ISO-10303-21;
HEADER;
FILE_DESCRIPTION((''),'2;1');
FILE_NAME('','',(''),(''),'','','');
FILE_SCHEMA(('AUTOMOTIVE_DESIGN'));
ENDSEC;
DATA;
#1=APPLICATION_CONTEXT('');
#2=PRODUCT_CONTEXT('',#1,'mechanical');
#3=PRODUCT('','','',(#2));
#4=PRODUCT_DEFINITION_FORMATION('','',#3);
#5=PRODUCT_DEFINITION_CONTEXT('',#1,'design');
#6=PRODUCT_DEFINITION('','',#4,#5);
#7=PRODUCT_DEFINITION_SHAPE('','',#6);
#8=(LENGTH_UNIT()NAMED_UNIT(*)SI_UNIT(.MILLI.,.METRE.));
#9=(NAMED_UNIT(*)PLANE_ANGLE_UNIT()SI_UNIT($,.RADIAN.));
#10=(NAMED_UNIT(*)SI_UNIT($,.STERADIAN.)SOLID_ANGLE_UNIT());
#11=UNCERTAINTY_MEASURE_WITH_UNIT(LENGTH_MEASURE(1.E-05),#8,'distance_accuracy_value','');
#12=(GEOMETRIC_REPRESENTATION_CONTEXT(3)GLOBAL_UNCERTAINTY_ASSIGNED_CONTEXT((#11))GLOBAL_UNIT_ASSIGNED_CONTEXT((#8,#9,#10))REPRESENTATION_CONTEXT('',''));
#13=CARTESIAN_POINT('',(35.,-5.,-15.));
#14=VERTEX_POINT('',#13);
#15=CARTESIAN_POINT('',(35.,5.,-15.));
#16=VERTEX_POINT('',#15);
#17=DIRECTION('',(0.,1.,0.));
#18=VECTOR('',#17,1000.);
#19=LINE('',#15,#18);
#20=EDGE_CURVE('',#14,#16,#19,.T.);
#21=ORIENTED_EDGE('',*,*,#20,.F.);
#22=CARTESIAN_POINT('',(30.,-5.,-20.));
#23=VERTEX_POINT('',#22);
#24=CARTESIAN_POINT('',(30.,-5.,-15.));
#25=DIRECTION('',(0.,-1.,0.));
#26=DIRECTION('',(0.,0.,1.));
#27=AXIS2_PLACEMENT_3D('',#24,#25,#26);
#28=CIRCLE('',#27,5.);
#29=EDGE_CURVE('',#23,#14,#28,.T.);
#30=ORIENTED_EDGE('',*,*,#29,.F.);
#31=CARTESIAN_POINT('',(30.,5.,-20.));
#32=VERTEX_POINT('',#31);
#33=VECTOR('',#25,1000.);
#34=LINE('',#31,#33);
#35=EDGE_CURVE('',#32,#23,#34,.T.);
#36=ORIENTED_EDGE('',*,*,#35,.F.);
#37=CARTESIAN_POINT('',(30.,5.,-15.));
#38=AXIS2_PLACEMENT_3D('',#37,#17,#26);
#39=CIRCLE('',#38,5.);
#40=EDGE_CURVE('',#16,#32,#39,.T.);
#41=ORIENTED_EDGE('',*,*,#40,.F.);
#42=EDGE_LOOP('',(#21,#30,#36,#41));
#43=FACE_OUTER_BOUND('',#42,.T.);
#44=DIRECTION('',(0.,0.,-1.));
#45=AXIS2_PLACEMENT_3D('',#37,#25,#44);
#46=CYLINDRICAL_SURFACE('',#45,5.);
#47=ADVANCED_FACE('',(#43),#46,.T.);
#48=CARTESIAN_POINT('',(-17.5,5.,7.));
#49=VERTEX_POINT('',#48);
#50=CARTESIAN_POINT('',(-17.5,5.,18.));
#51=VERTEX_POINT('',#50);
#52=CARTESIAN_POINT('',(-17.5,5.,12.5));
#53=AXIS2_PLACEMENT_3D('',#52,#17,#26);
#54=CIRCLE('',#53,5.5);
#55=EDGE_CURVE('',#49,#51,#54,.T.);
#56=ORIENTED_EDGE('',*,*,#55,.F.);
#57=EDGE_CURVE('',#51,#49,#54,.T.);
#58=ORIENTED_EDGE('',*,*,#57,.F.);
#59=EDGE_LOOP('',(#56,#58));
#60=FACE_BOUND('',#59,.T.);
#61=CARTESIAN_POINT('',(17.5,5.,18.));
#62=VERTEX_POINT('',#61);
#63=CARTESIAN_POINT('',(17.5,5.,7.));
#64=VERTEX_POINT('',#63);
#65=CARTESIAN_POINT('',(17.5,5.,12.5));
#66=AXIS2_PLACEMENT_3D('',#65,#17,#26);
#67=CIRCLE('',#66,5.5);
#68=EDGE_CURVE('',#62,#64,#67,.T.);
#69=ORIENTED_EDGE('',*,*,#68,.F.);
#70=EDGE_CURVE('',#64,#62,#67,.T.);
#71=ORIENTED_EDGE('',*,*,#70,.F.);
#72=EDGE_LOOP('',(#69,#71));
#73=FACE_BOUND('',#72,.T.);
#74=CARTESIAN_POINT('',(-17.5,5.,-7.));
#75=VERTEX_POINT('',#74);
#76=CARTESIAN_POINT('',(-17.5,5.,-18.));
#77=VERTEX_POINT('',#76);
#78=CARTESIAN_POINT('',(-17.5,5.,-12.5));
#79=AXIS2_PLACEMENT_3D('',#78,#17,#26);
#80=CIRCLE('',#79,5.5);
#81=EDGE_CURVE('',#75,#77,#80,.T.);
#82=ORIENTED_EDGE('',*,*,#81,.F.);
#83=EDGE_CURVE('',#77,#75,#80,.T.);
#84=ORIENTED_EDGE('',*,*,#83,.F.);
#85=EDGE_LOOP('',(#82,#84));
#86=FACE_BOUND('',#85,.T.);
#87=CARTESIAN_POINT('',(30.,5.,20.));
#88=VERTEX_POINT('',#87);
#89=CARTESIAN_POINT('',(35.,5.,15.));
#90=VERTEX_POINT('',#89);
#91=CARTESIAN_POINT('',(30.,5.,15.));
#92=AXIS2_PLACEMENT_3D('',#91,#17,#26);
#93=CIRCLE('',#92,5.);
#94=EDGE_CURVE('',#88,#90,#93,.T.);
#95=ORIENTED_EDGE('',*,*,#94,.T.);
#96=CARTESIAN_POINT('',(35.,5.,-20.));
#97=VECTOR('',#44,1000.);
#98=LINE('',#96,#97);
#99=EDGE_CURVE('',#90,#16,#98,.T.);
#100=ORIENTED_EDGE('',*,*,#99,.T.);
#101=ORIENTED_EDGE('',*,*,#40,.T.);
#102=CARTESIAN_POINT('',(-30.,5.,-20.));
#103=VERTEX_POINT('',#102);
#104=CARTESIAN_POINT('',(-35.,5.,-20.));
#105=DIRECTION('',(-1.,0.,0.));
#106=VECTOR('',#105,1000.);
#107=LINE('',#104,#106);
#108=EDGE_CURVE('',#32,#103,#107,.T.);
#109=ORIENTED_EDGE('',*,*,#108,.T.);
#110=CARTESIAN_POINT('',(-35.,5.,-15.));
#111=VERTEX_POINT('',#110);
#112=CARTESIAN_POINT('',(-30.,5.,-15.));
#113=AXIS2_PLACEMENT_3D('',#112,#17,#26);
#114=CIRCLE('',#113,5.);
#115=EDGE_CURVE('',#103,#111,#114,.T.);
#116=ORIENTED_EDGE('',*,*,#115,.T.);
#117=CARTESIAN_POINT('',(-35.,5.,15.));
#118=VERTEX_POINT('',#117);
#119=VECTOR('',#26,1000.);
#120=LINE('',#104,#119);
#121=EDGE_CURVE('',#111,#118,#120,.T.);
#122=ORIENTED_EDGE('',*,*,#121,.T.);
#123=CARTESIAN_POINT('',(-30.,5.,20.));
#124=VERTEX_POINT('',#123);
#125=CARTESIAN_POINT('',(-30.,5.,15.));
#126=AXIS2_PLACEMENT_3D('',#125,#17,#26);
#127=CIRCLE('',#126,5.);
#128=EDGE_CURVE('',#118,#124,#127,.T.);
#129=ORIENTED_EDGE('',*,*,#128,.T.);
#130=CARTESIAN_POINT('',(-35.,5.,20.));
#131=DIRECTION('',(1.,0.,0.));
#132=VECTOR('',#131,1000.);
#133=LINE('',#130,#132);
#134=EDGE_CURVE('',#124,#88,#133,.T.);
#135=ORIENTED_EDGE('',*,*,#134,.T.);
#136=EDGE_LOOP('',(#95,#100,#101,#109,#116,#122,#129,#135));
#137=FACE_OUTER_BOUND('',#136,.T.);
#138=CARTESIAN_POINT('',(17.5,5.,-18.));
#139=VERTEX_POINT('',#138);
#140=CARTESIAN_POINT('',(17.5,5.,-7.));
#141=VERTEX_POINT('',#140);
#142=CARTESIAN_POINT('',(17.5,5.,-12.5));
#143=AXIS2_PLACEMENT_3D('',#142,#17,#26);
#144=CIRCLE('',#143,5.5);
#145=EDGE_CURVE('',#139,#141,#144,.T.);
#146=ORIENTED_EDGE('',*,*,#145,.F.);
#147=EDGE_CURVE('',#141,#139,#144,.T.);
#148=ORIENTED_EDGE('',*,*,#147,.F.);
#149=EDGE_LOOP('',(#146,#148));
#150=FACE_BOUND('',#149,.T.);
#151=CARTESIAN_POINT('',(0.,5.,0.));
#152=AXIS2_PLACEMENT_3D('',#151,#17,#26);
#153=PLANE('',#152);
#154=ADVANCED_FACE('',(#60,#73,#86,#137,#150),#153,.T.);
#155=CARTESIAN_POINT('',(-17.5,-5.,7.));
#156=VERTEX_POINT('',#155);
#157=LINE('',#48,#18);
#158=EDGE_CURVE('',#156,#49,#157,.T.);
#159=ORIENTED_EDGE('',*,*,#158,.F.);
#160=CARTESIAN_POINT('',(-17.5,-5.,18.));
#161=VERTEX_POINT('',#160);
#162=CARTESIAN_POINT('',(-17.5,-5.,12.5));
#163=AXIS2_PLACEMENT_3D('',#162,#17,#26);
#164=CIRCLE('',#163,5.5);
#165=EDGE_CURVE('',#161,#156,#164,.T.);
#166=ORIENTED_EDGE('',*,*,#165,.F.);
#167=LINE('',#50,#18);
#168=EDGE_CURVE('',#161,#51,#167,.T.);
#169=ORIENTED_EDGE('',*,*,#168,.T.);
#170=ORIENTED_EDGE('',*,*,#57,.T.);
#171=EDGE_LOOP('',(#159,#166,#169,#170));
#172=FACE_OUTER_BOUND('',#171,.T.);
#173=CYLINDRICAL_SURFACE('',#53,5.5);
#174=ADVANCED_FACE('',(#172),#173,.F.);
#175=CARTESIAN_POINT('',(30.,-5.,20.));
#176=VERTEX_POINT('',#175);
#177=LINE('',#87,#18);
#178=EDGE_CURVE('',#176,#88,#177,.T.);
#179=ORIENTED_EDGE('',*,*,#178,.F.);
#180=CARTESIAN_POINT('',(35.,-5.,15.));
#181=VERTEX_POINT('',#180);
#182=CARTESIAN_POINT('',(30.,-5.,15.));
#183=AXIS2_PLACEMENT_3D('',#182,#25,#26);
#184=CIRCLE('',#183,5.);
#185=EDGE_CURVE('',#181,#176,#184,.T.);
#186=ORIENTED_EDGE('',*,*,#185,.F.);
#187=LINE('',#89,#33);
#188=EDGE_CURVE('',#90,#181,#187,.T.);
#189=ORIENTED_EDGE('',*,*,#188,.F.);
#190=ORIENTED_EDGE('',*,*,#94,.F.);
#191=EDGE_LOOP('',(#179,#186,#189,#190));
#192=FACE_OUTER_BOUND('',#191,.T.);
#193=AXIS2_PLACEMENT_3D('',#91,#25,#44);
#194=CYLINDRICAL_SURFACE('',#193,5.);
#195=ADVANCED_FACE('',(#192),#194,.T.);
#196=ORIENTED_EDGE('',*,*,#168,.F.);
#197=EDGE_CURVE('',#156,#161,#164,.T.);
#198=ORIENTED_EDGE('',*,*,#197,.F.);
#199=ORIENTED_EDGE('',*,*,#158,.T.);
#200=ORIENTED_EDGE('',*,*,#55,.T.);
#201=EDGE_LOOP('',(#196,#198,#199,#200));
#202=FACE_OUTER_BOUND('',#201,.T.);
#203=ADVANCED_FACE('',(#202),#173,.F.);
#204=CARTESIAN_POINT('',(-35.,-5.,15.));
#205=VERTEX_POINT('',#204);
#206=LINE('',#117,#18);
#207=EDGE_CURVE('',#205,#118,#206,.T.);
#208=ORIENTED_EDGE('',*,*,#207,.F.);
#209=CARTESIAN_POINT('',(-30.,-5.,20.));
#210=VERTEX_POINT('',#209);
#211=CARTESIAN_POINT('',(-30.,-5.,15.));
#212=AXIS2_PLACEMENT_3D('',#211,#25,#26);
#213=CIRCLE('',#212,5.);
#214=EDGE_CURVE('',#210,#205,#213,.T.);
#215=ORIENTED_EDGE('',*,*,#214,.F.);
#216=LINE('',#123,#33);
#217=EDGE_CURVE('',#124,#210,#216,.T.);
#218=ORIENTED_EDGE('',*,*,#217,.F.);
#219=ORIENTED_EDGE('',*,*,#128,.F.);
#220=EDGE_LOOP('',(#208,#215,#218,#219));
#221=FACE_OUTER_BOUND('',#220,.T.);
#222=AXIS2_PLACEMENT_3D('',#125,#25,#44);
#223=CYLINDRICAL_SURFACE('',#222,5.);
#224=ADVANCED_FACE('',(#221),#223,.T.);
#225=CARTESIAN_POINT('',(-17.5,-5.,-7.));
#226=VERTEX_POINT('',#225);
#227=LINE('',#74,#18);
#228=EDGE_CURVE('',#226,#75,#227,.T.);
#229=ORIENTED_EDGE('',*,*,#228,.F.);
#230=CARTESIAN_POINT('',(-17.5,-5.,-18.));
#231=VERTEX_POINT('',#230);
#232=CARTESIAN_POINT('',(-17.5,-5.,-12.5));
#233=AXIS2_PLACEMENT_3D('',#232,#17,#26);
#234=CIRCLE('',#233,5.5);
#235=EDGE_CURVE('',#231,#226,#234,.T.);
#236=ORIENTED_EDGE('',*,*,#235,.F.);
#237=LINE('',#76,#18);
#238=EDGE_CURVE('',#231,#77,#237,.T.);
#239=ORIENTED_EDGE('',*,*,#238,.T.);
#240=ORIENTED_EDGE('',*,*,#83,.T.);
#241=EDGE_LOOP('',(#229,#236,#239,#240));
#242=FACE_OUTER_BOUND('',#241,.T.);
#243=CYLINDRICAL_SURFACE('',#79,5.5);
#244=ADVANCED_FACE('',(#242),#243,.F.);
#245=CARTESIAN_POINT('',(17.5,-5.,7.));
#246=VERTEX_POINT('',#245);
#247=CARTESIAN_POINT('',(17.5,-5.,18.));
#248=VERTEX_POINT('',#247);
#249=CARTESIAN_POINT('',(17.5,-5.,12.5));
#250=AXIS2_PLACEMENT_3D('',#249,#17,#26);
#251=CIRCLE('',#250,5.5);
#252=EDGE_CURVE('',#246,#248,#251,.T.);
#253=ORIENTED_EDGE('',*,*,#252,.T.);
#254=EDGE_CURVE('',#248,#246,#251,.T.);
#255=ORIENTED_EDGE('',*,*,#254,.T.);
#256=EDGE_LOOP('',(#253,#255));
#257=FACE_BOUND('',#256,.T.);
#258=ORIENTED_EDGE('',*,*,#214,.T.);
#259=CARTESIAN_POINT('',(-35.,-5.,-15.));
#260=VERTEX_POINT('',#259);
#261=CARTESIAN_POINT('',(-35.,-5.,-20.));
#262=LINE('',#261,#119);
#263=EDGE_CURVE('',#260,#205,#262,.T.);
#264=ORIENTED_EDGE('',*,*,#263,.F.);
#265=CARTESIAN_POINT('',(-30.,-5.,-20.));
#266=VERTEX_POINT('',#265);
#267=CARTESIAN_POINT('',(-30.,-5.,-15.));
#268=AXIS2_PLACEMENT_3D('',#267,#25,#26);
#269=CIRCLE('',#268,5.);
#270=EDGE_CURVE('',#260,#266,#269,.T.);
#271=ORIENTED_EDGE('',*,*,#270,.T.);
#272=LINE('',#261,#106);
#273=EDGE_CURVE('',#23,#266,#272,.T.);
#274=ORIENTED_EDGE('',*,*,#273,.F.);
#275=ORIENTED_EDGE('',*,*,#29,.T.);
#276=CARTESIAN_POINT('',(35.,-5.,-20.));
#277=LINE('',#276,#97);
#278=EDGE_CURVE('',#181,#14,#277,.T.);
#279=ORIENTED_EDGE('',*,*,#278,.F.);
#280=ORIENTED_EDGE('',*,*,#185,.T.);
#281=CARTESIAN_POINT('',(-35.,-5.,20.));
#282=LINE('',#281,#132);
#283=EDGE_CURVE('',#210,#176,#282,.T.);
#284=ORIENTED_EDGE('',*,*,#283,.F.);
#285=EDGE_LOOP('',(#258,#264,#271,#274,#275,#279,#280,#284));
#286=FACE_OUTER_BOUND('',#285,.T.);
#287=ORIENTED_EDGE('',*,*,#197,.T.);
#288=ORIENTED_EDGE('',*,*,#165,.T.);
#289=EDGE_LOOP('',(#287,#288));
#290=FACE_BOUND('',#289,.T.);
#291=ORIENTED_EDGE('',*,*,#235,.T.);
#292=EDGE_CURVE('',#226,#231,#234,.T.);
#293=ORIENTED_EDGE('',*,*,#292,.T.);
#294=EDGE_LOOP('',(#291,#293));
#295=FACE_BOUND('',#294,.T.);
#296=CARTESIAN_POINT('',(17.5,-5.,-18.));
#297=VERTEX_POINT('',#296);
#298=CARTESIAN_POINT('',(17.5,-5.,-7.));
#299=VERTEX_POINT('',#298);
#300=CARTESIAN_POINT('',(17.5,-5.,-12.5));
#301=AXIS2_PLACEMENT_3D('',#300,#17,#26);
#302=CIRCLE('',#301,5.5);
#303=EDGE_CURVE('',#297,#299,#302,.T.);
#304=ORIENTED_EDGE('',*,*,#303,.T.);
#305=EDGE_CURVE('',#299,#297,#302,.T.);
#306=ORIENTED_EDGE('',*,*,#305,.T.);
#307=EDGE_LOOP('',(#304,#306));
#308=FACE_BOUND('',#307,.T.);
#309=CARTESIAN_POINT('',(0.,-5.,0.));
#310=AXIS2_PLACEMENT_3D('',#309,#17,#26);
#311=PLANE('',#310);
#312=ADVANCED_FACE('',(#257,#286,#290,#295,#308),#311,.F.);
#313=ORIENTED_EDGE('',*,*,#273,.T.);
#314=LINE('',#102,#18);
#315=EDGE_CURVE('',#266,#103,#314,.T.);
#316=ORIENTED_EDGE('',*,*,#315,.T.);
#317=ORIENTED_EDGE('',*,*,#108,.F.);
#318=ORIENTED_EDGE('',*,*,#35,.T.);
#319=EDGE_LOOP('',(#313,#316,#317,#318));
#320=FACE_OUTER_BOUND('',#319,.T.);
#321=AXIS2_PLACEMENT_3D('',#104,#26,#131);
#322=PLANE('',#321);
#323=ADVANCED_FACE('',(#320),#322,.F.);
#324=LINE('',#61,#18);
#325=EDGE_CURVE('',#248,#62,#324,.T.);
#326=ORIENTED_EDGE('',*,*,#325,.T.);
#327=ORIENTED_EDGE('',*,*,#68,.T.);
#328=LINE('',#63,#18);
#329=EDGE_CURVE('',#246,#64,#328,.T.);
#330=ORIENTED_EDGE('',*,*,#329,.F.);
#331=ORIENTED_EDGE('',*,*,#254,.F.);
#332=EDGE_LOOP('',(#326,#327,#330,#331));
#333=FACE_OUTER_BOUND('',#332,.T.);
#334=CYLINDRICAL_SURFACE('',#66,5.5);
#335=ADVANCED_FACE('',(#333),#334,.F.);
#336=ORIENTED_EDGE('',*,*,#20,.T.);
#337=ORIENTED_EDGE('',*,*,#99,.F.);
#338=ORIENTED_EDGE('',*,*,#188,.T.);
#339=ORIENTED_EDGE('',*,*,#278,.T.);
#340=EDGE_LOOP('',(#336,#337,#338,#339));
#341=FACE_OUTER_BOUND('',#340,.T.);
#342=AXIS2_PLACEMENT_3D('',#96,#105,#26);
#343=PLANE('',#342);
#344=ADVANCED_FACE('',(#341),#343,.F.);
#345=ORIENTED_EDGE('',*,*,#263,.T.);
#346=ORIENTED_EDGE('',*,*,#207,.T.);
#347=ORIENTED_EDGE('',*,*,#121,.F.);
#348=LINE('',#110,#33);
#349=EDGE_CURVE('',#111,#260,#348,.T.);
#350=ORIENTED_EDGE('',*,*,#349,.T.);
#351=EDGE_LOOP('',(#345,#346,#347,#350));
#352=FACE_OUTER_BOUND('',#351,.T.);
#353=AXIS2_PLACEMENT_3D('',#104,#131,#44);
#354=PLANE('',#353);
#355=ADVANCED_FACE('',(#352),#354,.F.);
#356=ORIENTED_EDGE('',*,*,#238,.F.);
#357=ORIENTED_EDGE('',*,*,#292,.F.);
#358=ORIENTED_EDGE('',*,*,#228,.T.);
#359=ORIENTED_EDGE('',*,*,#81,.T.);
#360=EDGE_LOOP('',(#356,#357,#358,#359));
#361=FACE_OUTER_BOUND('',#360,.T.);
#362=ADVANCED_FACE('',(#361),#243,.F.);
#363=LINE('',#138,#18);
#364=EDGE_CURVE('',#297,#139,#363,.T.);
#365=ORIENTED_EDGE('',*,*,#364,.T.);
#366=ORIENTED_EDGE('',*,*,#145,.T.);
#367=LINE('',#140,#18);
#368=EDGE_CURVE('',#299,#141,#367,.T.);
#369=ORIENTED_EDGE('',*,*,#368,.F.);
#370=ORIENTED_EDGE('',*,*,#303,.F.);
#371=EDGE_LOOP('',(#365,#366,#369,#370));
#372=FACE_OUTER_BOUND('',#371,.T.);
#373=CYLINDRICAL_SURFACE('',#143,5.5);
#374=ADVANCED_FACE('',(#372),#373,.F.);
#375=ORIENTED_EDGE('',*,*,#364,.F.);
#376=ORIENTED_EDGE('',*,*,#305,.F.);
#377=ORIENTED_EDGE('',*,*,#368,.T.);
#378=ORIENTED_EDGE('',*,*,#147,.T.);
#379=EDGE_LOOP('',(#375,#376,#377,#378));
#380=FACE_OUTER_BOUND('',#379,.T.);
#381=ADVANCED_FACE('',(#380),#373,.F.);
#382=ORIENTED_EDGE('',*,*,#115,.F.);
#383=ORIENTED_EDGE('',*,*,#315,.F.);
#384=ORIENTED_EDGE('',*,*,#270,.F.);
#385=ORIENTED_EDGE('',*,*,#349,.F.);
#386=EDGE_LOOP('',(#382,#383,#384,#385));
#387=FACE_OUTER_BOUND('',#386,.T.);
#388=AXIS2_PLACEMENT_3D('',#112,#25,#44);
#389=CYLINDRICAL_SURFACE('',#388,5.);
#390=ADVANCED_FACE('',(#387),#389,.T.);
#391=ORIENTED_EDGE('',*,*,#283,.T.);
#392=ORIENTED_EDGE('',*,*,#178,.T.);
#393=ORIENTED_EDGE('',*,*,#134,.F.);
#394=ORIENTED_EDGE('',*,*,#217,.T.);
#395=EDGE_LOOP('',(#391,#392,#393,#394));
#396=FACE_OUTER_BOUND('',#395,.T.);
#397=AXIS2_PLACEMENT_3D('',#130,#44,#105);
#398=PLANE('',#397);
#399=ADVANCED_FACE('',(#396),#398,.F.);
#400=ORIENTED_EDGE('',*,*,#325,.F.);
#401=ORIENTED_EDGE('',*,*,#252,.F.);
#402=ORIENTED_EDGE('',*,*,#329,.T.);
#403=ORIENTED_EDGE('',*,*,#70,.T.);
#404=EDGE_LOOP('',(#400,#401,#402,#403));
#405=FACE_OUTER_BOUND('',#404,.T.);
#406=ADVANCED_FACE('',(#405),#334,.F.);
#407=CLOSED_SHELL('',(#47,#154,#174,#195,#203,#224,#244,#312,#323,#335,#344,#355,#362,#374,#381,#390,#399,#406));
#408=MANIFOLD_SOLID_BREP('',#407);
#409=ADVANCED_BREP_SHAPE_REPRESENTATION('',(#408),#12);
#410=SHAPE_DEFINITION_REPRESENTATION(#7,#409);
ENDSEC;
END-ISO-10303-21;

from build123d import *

# Parameters (mm, degrees)
SKETCH_1_W          = 70
SKETCH_1_H          = 40
EXTRUDE_1_DEPTH     = 5
HOLE_WIZARD_M10_1_D = 11
FILLET_1_R          = 5


with BuildPart() as part:
    # 草图1 → 凸台-拉伸1 (new, symmetric)
    with BuildSketch(Plane(origin=(0, 0, 0), x_dir=(1, 0, 0), z_dir=(0, 1, 0))):
        Rectangle(SKETCH_1_W, SKETCH_1_H)
    extrude(amount=EXTRUDE_1_DEPTH, both=True)

    # M10 间隙孔1 (through all)
    with Locations(Plane(origin=(0, 5, 0), x_dir=(1, 0, 0), z_dir=(0, 1, 0))):
        with Locations((-17.5, 12.5), (17.5, 12.5), (17.5, -12.5), (-17.5, -12.5)):
            Hole(HOLE_WIZARD_M10_1_D / 2)

    # 圆角1
    fillet_1_edges = [part.edges().sort_by_distance(p)[0] for p in [
        (35, 0, 20),
        (-35, 0, 20),
        (-35, 0, -20),
        (35, 0, -20),
    ]]
    fillet(fillet_1_edges, radius=FILLET_1_R)


solid = part.part
